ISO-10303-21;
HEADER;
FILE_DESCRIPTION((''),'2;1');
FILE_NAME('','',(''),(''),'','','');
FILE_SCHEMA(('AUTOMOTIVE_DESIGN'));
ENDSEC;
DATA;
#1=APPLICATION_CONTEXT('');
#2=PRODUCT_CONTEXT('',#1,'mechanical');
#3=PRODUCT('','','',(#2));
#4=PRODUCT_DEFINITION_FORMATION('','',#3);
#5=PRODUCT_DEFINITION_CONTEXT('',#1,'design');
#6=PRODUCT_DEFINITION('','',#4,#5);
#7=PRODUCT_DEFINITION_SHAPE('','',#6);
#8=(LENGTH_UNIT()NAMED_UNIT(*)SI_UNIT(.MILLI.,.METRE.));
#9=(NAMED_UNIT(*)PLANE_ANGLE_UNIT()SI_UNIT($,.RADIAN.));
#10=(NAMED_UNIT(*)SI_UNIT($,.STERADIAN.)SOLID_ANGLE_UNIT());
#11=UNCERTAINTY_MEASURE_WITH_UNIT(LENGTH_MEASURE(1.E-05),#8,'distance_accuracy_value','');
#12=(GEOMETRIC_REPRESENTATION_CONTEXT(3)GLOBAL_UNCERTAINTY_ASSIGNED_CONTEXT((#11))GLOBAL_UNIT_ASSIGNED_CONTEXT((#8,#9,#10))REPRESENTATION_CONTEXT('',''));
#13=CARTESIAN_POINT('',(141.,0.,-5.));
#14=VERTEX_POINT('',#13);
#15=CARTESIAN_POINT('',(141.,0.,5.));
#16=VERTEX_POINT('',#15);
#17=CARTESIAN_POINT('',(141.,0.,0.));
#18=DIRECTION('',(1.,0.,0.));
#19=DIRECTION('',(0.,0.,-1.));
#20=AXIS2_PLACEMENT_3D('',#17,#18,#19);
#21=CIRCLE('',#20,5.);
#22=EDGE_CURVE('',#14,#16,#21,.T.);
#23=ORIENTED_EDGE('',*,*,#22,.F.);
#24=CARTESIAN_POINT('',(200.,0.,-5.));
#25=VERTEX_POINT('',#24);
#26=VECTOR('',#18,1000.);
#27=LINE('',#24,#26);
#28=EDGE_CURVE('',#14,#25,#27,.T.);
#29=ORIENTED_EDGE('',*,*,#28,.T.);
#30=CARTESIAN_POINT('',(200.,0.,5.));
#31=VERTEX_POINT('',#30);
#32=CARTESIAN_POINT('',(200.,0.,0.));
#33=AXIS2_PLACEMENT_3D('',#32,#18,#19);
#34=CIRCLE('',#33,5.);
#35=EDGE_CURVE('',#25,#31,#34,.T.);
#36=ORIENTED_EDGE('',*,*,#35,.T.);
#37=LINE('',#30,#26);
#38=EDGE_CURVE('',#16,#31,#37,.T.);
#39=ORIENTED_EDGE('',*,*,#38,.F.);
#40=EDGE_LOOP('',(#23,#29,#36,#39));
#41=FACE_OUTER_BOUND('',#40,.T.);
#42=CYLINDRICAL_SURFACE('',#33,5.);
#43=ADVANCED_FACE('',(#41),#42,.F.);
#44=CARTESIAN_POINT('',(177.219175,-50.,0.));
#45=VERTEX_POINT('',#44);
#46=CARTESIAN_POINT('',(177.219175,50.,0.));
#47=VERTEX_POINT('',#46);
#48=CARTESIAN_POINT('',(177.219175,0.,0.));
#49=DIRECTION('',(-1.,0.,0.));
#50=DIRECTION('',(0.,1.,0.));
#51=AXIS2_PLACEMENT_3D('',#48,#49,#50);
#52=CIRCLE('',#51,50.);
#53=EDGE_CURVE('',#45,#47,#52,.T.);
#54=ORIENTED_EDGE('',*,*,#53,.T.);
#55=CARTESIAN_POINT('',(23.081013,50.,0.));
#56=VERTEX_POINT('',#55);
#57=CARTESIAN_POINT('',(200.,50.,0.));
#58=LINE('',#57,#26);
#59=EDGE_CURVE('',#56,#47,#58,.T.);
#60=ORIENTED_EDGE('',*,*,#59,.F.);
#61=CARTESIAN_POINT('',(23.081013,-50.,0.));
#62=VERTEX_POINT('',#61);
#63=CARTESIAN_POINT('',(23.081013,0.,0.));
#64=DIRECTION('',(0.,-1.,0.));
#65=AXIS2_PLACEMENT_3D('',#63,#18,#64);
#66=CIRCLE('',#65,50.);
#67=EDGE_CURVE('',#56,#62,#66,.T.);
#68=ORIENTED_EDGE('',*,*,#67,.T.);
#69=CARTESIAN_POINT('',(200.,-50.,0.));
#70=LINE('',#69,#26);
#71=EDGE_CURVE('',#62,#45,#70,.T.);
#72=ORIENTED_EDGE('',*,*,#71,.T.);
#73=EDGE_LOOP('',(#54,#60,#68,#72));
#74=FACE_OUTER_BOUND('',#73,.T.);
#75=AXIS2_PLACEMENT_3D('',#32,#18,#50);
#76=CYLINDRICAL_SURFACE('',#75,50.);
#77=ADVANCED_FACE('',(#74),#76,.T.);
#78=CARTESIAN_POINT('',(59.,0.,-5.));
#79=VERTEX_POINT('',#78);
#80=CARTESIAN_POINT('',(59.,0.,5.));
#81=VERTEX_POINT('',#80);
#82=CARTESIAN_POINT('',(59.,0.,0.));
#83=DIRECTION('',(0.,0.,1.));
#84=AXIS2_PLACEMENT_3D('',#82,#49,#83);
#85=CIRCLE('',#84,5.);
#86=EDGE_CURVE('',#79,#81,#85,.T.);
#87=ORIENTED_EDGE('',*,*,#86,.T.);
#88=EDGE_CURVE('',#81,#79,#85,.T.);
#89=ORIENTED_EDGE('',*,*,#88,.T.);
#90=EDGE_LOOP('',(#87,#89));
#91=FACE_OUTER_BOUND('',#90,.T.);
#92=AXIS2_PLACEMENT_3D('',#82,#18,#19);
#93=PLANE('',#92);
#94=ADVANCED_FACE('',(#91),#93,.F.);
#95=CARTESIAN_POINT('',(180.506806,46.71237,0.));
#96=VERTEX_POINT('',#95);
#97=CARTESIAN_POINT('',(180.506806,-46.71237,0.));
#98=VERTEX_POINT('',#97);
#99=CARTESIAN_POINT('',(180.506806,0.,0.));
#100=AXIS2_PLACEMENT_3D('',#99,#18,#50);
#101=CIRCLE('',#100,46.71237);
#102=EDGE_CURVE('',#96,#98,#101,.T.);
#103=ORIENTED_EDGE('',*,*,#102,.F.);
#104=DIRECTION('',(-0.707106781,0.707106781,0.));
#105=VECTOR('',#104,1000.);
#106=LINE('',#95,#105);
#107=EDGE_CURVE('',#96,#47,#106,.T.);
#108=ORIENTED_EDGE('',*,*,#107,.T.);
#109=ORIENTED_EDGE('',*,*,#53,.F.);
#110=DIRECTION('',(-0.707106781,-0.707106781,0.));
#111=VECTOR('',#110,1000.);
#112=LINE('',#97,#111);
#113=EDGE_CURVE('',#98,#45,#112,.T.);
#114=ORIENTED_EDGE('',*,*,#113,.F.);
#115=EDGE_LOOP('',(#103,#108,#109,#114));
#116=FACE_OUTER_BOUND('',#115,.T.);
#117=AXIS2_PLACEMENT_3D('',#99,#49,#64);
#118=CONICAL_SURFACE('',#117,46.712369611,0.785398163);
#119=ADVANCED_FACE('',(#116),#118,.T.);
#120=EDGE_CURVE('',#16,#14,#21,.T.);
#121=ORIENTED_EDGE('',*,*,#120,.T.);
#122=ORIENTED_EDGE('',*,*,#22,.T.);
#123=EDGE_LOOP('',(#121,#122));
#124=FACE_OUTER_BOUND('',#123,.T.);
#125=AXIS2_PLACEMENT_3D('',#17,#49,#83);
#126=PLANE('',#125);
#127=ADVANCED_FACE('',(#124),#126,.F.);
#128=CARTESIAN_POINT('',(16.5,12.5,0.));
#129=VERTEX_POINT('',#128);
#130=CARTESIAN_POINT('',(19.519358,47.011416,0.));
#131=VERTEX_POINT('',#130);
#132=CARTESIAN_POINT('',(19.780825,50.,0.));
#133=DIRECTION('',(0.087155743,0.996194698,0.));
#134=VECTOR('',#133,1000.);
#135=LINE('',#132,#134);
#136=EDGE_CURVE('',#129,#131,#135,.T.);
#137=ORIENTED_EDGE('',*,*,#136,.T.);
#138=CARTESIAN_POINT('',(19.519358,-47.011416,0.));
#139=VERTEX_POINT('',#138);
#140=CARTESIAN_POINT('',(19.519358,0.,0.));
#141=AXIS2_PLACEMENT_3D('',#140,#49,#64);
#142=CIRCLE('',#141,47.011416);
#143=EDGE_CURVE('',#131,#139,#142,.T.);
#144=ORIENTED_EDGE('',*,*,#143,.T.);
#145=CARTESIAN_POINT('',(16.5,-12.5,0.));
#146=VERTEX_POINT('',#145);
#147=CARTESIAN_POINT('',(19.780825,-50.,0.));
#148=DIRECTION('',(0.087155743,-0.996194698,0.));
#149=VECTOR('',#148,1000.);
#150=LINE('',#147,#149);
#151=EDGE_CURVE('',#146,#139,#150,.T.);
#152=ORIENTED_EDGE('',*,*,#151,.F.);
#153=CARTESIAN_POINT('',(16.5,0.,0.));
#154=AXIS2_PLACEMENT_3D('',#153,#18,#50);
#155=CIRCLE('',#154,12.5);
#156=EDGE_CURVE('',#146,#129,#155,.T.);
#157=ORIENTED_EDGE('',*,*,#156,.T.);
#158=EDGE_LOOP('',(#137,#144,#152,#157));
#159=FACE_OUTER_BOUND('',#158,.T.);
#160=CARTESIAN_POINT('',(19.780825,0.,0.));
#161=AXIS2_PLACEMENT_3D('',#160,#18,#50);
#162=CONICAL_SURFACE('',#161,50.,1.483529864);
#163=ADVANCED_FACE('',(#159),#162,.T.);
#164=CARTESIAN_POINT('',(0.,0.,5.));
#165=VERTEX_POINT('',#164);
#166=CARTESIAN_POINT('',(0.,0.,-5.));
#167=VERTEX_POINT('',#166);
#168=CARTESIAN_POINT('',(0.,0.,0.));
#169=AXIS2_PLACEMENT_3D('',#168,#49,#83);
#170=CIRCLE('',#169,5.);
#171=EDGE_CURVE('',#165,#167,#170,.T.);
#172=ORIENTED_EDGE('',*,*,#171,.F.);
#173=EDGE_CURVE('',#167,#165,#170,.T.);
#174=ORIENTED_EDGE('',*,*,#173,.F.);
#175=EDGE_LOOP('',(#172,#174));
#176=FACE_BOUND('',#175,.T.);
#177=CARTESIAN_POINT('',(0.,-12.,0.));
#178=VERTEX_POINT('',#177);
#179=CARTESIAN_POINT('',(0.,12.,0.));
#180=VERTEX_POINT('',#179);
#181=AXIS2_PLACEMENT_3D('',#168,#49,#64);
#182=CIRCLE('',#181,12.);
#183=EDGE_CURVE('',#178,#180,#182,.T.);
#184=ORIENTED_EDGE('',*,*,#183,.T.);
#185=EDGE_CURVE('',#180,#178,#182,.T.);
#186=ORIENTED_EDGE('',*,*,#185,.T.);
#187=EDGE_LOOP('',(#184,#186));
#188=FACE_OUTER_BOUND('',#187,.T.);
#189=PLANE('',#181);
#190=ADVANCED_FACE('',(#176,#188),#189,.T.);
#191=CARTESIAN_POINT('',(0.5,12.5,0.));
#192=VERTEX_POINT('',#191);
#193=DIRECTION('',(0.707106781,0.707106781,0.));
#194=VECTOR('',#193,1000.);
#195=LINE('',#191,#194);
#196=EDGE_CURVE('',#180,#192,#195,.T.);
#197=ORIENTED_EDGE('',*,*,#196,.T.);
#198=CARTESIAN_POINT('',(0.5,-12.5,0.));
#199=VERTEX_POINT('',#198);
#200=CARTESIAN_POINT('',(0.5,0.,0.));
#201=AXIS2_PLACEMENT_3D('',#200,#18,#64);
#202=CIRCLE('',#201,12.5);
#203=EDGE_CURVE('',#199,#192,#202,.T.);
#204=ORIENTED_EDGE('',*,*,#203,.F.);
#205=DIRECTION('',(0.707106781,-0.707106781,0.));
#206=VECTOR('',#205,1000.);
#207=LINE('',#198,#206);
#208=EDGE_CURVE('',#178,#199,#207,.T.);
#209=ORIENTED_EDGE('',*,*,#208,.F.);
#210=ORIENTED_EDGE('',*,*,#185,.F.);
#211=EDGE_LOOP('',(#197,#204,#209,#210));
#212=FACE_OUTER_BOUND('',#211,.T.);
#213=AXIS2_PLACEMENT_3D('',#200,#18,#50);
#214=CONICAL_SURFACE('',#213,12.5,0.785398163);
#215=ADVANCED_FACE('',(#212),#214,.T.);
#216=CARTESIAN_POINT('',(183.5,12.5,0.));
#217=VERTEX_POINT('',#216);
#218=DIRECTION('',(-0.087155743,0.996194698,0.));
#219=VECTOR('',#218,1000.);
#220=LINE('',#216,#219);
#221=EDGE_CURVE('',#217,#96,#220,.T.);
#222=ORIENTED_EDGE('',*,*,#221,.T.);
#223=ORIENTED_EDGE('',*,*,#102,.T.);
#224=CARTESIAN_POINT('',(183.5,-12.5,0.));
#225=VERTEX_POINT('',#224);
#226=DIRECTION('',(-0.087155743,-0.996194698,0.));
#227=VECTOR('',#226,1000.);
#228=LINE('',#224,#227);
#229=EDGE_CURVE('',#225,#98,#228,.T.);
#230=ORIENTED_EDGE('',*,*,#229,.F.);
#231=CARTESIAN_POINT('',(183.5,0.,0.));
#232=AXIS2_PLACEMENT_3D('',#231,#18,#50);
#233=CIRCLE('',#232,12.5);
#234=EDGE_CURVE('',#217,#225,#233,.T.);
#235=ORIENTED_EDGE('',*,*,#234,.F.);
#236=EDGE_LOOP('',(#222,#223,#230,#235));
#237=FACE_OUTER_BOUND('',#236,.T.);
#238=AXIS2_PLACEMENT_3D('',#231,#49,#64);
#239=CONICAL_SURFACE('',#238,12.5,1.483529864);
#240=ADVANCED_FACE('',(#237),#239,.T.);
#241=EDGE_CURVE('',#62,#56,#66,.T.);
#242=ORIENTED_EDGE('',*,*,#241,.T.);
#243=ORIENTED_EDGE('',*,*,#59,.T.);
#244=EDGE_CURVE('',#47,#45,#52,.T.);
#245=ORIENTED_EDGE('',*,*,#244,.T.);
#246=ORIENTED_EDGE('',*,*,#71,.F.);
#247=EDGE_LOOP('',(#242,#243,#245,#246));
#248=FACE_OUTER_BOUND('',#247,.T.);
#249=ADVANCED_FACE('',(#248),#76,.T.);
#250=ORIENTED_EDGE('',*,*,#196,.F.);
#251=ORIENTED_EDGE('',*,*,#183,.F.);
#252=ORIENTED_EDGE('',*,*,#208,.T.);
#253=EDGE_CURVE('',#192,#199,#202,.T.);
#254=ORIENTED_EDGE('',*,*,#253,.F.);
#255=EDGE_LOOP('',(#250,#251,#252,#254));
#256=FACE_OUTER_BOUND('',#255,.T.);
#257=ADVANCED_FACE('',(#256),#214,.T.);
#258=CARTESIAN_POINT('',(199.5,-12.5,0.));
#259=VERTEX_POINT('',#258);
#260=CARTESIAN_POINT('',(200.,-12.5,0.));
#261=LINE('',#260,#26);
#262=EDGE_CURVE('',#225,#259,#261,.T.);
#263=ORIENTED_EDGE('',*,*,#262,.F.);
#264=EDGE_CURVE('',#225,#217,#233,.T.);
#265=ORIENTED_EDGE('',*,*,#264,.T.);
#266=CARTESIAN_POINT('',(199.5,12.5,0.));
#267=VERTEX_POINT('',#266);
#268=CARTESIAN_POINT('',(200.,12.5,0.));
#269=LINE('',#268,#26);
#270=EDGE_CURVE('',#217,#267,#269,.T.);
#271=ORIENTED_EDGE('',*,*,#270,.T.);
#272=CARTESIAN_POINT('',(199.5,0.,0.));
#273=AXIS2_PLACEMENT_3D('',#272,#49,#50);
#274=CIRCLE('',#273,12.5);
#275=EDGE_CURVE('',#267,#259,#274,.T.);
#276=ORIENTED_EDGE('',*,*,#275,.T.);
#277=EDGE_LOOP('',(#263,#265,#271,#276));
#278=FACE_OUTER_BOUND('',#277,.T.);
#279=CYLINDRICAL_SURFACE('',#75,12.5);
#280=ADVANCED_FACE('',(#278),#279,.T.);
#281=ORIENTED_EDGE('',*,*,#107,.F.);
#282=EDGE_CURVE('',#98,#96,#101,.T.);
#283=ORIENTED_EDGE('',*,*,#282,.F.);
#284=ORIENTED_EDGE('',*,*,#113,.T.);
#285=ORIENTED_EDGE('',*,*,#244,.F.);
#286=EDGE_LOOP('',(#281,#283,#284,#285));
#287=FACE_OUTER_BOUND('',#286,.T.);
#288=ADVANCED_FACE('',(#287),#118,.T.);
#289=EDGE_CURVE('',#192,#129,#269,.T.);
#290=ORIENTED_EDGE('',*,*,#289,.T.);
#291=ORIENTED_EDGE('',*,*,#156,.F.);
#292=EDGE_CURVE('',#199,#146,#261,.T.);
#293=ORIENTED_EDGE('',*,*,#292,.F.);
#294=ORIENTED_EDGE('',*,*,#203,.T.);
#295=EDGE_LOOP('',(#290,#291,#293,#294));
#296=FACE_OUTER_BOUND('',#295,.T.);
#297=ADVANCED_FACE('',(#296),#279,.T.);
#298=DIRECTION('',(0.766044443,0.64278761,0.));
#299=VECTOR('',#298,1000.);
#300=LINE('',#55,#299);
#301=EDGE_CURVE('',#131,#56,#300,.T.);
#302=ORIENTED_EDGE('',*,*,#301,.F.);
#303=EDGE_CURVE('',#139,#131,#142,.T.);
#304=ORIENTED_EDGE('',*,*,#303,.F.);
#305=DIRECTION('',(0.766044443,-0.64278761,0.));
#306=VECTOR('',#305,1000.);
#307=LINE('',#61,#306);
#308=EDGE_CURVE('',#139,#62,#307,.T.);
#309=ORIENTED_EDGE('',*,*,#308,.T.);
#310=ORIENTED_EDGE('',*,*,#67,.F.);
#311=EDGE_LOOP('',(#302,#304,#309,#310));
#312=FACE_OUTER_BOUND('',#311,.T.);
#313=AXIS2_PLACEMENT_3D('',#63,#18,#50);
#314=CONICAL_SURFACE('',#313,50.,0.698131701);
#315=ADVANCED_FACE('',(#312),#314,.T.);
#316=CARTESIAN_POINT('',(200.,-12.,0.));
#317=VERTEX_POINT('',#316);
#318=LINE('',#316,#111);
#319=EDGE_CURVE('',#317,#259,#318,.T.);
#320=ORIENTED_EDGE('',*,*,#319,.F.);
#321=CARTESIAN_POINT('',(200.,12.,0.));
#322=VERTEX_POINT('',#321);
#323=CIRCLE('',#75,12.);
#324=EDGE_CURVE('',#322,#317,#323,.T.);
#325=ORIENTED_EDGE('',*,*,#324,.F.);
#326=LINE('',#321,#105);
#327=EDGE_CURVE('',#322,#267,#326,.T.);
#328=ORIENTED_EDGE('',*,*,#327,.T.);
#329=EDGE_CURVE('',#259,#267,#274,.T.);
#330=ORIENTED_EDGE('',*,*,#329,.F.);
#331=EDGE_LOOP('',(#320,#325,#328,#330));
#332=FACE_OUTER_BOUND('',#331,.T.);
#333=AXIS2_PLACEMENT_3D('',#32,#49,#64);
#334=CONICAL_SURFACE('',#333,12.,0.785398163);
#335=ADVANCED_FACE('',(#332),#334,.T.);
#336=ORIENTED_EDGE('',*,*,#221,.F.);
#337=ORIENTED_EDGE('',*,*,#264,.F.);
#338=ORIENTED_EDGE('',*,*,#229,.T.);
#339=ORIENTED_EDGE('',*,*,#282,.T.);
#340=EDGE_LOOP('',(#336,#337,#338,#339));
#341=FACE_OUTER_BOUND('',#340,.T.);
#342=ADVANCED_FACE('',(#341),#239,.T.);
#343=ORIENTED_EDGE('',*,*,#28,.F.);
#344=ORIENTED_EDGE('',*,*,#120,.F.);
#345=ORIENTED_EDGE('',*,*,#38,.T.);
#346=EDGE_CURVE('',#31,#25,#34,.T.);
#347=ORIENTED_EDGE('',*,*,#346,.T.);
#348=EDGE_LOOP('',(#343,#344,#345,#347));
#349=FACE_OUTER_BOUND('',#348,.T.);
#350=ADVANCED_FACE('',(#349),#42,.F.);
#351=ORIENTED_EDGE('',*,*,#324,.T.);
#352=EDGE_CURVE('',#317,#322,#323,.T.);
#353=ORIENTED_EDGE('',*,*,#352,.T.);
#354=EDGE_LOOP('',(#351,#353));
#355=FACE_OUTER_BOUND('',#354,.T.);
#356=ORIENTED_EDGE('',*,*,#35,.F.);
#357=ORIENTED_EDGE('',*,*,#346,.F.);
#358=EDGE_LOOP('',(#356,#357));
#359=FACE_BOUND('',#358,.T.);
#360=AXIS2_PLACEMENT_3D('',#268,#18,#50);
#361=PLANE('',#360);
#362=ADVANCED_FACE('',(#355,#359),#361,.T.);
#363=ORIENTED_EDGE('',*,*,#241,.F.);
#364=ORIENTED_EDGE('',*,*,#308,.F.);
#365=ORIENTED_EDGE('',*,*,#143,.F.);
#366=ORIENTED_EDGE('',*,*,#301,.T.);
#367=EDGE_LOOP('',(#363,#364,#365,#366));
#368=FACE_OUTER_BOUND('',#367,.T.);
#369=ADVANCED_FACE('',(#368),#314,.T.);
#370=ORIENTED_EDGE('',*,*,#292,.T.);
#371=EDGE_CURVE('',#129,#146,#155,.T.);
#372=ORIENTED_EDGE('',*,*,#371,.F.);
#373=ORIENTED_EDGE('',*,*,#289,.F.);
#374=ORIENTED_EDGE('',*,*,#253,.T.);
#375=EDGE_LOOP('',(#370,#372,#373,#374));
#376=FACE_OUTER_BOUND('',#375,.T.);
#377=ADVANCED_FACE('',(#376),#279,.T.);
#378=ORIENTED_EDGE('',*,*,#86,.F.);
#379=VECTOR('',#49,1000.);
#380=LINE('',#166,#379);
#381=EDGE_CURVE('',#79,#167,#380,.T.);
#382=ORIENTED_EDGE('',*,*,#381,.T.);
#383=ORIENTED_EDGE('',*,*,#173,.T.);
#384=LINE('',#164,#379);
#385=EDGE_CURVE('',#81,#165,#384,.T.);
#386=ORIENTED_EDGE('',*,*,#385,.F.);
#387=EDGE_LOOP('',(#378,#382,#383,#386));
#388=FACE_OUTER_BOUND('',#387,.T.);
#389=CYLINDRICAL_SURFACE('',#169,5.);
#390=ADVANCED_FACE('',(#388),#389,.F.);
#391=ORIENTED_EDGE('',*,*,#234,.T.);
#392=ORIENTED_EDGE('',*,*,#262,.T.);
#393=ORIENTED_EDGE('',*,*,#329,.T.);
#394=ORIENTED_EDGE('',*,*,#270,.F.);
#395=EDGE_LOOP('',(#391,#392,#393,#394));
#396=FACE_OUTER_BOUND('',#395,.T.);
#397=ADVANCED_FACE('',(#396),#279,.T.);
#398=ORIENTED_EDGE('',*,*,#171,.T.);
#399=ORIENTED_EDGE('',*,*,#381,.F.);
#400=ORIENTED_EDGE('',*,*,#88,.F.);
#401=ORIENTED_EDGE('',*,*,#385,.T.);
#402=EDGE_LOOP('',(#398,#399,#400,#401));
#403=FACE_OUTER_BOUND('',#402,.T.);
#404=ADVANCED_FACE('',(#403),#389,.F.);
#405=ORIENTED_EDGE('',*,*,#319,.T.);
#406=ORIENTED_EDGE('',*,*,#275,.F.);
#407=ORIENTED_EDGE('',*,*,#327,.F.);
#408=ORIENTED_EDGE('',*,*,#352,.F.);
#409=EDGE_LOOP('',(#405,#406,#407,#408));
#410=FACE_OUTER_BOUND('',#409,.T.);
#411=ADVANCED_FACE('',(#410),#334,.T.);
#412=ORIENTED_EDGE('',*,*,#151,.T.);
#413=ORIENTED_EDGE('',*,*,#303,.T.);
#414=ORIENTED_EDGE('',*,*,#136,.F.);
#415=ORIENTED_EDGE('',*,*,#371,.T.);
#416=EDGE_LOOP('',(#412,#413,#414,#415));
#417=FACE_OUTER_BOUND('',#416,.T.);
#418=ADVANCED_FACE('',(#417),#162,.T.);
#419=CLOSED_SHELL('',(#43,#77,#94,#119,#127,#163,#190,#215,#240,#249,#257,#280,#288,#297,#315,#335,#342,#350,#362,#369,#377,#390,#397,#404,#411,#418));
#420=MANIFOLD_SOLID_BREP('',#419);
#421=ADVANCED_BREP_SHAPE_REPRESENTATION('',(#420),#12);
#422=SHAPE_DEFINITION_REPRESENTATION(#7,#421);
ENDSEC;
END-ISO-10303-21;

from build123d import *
from OCP.BRepFilletAPI import BRepFilletAPI_MakeChamfer

# Parameters (mm, degrees)
JOURNAL_CHAMFER_0_5MM_A_SIZE  = 0.5
JOURNAL_CHAMFER_0_5MM_B_SIZE  = 0.5
BODY_EDGE_CHAMFER_3MM_SIZE    = 3
BODY_EDGE_CHAMFER_3MM_SIZE2   = 3.300188603
CENTRE_HOLE_10X59_END_A_D     = 10
CENTRE_HOLE_10X59_END_A_DEPTH = 59
CENTRE_HOLE_10X59_END_B_D     = 10
CENTRE_HOLE_10X59_END_B_DEPTH = 59


with BuildPart() as part:
    # Roller Profile Sketch → Roller Body (revolve)
    with BuildSketch(Plane.XY):
        Polygon((0, 0), (0, 12.5), (16.5, 12.5), (19.780824882, 50), (180.219175118, 50), (183.5, 12.5), (200, 12.5), (200, 0), align=None)
    revolve(axis=Axis((200, 0, 0), (-1, 0, 0)))

    # Journal Chamfer 0.5mm A
    journal_chamfer_0_5mm_a_edges = [part.edges().sort_by_distance(p)[0] for p in [
        (200, -12.5, 0),
    ]]
    chamfer(journal_chamfer_0_5mm_a_edges, length=JOURNAL_CHAMFER_0_5MM_A_SIZE)

    # Journal Chamfer 0.5mm B
    journal_chamfer_0_5mm_b_edges = [part.edges().sort_by_distance(p)[0] for p in [
        (0, -12.5, 0),
    ]]
    chamfer(journal_chamfer_0_5mm_b_edges, length=JOURNAL_CHAMFER_0_5MM_B_SIZE)

    # Body Edge Chamfer 3mm: one chamfer whose edges measure the first distance from different faces: ONE call of the kernel's chamfer builder (chamfer() names one face for all edges)
    body_edge_chamfer_3mm_edges_1 = [part.edges().sort_by_distance(p)[0] for p in [
        (180.219175118, -50, 0),
    ]]
    body_edge_chamfer_3mm_side_1 = [part.faces().sort_by_distance(p)[0] for p in [
        (100, -50, 0),
    ]]
    body_edge_chamfer_3mm_edges_2 = [part.edges().sort_by_distance(p)[0] for p in [
        (19.780824882, -50, 0),
    ]]
    body_edge_chamfer_3mm_side_2 = [part.faces().sort_by_distance(p)[0] for p in [
        (18.140412441, -31.25, 0),
    ]]
    body_edge_chamfer_3mm = BRepFilletAPI_MakeChamfer(part.part.solid().wrapped)
    for e in body_edge_chamfer_3mm_edges_1:
        body_edge_chamfer_3mm.Add(BODY_EDGE_CHAMFER_3MM_SIZE, BODY_EDGE_CHAMFER_3MM_SIZE2, e.wrapped, body_edge_chamfer_3mm_side_1[0].wrapped)  # the first distance lies on this face
    for e in body_edge_chamfer_3mm_edges_2:
        body_edge_chamfer_3mm.Add(BODY_EDGE_CHAMFER_3MM_SIZE, BODY_EDGE_CHAMFER_3MM_SIZE2, e.wrapped, body_edge_chamfer_3mm_side_2[0].wrapped)  # the first distance lies on this face
    add(Compound.cast(body_edge_chamfer_3mm.Shape()), mode=Mode.REPLACE)

    # Centre Hole Ø10x59 End A
    with Locations(Plane(origin=(200, 0, 0), x_dir=(0, 0, -1), z_dir=(1, 0, 0))):
        with Locations((0, 0)):
            Hole(CENTRE_HOLE_10X59_END_A_D / 2, depth=CENTRE_HOLE_10X59_END_A_DEPTH)

    # Centre Hole Ø10x59 End B
    with Locations(Plane.ZY):
        with Locations((0, 0)):
            Hole(CENTRE_HOLE_10X59_END_B_D / 2, depth=CENTRE_HOLE_10X59_END_B_DEPTH)


solid = part.part
